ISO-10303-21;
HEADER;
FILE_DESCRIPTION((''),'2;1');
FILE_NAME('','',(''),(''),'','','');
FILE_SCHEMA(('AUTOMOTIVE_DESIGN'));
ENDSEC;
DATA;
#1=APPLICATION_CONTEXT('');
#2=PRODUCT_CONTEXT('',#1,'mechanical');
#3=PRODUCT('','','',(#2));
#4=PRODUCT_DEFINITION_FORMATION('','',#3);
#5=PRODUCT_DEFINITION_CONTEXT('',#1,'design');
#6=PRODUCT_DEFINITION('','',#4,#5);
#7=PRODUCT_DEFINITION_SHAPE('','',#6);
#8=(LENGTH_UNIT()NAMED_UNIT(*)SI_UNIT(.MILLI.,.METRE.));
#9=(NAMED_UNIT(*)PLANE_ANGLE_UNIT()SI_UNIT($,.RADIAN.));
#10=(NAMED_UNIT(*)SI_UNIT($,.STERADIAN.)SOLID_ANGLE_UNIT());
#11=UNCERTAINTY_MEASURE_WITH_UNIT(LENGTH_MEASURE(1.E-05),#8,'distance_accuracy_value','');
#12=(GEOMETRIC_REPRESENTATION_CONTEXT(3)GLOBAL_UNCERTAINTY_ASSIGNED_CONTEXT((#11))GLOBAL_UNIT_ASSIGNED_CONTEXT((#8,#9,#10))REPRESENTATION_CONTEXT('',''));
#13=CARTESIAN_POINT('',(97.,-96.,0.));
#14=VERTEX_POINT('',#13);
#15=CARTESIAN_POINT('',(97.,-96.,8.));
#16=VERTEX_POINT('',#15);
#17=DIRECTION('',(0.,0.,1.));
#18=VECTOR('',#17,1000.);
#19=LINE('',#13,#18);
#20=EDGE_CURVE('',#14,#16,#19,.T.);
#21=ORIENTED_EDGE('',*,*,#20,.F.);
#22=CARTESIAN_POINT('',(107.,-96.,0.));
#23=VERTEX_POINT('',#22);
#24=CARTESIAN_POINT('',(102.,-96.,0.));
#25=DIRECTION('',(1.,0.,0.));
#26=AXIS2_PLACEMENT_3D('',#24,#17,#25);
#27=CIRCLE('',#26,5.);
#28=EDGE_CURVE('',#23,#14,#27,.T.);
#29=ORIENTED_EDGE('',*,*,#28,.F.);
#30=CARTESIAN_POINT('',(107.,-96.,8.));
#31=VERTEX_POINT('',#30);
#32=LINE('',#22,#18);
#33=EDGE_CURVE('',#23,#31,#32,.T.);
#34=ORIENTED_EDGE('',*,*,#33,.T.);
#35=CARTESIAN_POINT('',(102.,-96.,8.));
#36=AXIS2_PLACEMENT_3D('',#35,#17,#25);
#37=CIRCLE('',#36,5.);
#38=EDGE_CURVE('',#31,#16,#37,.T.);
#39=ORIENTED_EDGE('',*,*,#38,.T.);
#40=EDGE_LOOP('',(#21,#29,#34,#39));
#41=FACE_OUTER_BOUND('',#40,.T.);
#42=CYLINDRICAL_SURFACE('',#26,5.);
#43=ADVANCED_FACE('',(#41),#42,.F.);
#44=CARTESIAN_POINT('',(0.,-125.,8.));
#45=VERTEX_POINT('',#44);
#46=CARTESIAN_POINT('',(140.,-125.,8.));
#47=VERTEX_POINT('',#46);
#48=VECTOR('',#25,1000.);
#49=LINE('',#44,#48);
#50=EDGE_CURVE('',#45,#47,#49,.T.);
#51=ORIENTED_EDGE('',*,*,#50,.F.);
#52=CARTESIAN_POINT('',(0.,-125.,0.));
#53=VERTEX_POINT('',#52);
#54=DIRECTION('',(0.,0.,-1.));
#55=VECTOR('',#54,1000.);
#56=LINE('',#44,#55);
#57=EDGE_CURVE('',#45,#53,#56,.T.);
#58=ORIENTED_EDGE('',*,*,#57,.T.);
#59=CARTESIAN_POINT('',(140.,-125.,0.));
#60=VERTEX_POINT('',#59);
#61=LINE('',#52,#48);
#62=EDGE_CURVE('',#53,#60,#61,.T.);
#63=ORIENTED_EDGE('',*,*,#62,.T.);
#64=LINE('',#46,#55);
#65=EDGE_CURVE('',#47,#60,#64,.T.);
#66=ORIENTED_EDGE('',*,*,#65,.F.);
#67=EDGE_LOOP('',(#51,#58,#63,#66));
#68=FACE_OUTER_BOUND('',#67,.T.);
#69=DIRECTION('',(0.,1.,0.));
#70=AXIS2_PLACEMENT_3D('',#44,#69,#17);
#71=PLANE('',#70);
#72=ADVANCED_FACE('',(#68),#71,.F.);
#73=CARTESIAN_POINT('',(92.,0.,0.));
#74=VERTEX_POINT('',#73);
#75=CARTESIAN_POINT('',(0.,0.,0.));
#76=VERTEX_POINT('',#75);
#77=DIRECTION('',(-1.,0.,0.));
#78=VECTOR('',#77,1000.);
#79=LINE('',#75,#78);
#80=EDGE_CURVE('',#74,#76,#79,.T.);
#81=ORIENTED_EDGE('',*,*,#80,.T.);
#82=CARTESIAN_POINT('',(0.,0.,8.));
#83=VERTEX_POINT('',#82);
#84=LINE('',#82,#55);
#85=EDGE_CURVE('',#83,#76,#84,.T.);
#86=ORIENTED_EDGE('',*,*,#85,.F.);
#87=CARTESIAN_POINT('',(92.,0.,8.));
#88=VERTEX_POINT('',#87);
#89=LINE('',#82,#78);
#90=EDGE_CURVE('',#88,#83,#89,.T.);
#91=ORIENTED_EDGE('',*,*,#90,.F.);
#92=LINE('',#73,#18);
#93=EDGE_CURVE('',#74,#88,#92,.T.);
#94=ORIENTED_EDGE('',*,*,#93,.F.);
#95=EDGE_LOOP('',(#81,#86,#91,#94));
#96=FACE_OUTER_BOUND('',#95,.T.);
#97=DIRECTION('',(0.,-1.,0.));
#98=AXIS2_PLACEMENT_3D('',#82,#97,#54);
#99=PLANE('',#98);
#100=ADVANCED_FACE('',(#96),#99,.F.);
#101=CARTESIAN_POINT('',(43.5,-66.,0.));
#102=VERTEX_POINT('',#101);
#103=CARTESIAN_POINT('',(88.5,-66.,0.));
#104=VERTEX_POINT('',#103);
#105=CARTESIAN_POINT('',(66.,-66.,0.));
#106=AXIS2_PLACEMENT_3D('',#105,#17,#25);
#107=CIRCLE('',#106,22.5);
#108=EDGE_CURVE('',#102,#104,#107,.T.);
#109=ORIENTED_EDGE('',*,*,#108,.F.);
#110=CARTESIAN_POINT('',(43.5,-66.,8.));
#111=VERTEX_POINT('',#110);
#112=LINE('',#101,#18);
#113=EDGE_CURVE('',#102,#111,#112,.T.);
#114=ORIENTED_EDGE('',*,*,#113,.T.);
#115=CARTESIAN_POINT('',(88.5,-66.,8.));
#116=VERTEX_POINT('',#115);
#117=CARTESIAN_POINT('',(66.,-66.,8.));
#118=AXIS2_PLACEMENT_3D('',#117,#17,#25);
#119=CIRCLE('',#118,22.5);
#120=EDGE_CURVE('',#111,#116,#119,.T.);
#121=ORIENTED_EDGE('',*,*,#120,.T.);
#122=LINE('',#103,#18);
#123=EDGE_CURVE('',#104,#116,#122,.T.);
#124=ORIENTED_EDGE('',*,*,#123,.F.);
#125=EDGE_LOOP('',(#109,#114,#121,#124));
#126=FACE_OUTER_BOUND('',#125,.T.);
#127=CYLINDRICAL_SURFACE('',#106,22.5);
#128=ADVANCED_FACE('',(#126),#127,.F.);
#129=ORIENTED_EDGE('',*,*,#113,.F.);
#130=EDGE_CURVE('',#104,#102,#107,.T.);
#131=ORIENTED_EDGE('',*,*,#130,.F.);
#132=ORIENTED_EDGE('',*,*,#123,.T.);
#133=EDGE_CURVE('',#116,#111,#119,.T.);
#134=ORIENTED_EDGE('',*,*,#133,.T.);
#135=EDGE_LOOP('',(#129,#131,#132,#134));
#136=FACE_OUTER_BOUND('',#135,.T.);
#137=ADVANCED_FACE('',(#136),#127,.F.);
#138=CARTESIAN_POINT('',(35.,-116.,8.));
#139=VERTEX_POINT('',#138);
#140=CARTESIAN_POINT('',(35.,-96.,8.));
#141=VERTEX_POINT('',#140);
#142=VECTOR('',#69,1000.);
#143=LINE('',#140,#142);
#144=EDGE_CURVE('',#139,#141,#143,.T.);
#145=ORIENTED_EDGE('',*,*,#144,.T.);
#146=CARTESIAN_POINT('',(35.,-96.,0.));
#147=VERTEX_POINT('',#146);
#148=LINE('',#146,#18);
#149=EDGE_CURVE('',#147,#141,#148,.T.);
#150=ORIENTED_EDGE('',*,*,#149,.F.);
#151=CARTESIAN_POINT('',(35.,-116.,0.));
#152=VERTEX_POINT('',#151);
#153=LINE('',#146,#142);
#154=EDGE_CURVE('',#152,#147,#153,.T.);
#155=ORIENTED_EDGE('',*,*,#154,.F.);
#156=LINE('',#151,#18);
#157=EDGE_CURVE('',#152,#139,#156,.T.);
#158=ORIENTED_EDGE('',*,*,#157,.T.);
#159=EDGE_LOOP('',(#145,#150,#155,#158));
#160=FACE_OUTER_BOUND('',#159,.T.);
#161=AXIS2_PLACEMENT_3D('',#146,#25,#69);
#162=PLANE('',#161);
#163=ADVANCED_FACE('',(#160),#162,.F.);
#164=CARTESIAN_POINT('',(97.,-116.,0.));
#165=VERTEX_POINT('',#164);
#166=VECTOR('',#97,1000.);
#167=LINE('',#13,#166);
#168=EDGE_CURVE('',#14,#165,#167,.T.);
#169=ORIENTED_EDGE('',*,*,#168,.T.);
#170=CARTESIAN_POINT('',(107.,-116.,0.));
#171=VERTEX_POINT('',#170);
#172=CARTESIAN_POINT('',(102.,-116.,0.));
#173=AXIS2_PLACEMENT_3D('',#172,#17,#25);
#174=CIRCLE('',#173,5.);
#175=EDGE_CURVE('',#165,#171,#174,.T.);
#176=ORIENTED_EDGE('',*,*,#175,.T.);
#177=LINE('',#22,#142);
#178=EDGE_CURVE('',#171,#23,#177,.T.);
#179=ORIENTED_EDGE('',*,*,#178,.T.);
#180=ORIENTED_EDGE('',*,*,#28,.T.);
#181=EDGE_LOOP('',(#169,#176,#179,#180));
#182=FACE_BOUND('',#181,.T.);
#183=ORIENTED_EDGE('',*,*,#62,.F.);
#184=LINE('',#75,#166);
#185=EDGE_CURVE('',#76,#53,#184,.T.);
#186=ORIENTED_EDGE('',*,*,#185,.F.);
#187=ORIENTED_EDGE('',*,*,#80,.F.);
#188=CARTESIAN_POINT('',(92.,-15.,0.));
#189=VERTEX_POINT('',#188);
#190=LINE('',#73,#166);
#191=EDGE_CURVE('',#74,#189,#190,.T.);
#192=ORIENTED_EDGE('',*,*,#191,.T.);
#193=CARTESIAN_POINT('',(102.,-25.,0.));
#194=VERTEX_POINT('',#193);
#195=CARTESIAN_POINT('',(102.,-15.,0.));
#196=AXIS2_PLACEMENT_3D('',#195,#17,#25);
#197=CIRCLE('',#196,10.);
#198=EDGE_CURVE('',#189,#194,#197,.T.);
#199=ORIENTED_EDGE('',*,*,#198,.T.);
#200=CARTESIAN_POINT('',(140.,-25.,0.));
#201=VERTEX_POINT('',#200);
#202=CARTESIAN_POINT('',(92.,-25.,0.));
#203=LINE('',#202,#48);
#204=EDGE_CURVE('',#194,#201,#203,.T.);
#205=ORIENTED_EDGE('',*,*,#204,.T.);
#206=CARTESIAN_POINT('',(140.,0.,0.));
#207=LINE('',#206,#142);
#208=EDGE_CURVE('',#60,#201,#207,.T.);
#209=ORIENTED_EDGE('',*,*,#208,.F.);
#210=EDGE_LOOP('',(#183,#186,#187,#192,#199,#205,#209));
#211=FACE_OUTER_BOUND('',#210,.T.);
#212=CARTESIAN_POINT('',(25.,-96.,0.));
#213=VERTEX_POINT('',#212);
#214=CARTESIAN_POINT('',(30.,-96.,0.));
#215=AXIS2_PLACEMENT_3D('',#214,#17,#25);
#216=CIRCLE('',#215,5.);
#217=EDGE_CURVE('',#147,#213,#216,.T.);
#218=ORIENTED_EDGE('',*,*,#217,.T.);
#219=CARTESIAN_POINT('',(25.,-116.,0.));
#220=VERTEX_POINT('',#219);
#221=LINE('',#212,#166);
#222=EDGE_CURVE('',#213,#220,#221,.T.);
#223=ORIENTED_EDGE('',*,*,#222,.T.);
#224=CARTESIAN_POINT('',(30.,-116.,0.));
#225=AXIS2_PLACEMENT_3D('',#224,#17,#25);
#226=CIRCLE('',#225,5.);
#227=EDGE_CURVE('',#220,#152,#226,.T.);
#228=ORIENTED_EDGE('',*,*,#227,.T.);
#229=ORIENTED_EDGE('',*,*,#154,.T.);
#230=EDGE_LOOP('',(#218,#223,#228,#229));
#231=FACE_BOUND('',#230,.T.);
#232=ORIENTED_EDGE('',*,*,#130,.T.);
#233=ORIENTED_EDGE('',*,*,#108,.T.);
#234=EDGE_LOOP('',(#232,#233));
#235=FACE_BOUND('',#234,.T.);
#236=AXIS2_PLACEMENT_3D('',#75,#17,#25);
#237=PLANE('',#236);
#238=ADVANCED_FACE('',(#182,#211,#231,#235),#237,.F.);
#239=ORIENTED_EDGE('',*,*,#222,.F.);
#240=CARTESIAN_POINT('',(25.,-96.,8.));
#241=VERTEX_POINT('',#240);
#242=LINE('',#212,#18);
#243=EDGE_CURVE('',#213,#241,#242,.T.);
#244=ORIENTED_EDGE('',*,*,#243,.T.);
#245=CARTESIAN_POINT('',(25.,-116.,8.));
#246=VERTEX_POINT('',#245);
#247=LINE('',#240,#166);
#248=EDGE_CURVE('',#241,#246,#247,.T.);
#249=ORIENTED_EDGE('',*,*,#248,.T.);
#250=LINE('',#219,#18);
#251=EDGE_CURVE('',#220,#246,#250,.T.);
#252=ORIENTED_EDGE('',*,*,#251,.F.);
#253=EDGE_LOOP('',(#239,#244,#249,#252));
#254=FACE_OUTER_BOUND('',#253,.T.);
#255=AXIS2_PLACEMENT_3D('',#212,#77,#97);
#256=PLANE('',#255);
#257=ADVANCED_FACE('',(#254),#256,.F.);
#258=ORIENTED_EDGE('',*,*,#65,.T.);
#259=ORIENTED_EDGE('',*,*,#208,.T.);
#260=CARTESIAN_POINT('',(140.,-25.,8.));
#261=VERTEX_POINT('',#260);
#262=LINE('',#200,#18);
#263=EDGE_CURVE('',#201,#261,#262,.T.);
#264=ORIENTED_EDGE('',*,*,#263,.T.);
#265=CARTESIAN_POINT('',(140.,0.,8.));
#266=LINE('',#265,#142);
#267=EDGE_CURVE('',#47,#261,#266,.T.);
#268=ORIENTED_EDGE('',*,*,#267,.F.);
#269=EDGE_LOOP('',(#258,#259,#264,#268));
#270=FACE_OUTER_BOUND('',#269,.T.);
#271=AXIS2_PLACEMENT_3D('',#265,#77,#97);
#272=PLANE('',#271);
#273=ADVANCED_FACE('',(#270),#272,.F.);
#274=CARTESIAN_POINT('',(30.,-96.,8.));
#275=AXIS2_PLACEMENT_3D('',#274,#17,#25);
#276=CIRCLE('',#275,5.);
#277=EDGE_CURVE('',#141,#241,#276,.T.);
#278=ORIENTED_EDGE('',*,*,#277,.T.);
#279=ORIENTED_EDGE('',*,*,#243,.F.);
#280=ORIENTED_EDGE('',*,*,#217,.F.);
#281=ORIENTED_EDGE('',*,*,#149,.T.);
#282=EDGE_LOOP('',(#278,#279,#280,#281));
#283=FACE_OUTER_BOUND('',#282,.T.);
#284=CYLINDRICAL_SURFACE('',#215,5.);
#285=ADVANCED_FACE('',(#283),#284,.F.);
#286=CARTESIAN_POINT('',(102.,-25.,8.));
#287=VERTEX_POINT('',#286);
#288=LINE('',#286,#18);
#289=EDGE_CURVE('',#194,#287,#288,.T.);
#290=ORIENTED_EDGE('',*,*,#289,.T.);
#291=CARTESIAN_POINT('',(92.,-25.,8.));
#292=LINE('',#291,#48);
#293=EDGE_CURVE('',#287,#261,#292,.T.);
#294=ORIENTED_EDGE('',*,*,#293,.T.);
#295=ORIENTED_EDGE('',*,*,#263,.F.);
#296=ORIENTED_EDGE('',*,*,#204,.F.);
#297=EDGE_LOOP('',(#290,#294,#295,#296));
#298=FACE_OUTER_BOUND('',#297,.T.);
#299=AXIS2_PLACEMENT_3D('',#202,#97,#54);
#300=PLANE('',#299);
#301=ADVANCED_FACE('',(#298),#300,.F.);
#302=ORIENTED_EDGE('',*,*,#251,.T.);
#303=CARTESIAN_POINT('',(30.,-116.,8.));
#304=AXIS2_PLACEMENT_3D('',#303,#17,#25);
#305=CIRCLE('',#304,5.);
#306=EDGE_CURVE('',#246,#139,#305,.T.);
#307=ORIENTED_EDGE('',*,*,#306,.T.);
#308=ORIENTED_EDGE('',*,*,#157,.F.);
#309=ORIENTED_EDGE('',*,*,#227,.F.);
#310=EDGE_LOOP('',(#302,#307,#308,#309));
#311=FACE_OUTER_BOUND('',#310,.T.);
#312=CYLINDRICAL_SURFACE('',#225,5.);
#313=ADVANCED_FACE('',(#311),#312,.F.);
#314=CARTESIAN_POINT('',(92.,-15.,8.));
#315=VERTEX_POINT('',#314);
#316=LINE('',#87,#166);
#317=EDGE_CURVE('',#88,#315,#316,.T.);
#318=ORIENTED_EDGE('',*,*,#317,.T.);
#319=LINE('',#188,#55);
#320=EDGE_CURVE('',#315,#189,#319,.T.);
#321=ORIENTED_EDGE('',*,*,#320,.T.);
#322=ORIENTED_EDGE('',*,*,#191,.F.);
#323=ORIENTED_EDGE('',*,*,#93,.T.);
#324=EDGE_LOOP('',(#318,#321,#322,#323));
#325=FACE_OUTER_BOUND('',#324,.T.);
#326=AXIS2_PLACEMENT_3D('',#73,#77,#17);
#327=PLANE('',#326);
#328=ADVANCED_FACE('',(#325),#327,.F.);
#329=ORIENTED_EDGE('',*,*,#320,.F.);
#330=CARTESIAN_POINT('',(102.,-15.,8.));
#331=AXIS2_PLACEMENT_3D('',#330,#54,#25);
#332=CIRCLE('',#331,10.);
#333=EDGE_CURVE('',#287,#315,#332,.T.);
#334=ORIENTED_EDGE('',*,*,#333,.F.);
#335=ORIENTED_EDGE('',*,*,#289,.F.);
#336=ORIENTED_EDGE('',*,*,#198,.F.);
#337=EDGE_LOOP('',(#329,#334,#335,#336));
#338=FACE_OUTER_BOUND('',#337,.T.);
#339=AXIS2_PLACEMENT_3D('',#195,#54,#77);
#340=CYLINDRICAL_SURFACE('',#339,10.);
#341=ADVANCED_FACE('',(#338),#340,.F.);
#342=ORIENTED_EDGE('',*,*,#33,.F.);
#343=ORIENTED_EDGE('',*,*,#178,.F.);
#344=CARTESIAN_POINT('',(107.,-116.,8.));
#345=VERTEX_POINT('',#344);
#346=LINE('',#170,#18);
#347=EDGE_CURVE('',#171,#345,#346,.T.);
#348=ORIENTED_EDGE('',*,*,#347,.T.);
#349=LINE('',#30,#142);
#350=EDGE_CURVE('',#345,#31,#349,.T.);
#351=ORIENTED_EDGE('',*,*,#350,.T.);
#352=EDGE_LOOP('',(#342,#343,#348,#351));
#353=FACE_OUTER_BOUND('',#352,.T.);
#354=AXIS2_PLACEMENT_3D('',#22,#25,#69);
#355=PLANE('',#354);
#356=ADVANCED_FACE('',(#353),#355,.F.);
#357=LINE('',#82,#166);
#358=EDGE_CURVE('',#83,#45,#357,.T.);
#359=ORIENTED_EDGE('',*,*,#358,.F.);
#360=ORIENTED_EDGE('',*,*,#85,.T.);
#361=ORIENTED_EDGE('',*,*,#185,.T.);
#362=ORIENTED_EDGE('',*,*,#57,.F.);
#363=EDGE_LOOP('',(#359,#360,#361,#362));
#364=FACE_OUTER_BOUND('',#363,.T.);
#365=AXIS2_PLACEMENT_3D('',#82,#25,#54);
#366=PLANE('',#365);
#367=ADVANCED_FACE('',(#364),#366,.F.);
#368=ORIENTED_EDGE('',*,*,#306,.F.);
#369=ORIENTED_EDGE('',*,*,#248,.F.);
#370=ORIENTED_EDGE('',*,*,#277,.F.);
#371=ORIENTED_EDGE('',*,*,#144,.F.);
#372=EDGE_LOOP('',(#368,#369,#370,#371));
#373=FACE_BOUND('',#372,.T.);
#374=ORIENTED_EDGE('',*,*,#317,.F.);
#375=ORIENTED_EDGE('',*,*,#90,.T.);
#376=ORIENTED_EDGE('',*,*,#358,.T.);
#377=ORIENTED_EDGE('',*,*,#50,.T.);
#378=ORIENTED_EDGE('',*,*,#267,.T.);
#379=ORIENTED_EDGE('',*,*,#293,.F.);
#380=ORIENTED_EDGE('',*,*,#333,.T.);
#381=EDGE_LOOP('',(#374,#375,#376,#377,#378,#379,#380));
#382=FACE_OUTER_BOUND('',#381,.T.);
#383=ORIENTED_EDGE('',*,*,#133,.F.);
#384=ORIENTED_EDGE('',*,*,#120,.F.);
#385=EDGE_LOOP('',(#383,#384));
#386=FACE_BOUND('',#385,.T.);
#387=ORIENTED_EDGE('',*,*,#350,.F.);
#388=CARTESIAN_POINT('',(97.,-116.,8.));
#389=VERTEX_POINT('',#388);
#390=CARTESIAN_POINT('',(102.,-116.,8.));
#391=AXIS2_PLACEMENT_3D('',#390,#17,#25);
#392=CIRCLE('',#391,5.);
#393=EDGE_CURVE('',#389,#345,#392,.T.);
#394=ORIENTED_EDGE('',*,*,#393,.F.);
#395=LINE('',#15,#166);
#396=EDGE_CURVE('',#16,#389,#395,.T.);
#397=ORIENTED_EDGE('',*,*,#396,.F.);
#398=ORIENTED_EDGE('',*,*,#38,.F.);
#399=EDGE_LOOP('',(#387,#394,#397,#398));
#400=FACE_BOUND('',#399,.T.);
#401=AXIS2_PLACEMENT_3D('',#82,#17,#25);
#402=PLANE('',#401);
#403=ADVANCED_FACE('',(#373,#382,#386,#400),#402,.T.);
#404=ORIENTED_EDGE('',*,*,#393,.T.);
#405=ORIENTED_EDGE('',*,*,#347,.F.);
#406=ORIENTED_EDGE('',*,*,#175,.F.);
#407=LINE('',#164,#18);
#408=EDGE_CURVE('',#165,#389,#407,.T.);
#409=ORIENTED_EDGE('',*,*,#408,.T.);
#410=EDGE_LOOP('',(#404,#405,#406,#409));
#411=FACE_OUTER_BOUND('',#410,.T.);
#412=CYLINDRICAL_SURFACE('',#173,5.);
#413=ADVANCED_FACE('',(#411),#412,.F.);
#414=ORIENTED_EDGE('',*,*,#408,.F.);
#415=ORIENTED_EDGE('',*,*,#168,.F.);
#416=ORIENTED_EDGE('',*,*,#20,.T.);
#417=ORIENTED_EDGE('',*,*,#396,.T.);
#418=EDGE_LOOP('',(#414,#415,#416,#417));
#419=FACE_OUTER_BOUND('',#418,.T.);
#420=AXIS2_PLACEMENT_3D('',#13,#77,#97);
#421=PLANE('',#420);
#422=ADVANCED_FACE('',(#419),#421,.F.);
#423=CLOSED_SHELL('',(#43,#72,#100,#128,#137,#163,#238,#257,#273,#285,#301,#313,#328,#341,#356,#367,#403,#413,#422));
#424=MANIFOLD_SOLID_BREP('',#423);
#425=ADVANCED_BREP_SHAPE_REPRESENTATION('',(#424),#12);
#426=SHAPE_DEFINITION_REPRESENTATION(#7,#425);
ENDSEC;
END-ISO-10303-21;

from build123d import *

# Parameters (mm, degrees)
SKETCH1_W           = 140
SKETCH1_H           = 125
BOSS_EXTRUDE1_DEPTH = 8
SKETCH2_R           = 22.5
CUT_EXTRUDE1_DEPTH  = 8
CUT_EXTRUDE2_DEPTH  = 8
LPATTERN1_COUNT     = 2
LPATTERN1_PITCH     = 72
SKETCH4_W           = 48
SKETCH4_H           = 25
CUT_EXTRUDE3_DEPTH  = 8
FILLET1_R           = 10


with BuildPart() as part:
    # Sketch1 → Boss-Extrude1 (new body)
    with BuildSketch(Plane.XY):
        with Locations((70, -62.5)):
            Rectangle(SKETCH1_W, SKETCH1_H)
    extrude(amount=BOSS_EXTRUDE1_DEPTH)

    # Sketch2 → Cut-Extrude1 (cut)
    with BuildSketch(Plane.XY.offset(8)):
        with Locations((66, -66)):
            Circle(SKETCH2_R)
    extrude(amount=-CUT_EXTRUDE1_DEPTH, mode=Mode.SUBTRACT)

    # Sketch3 → Cut-Extrude2 (cut)
    with BuildSketch(Plane.XY.offset(8)):
        with BuildLine():
            Line((35, -96), (35, -116))
            ThreePointArc((35, -116), (30, -121), (25, -116))
            Line((25, -116), (25, -96))
            ThreePointArc((25, -96), (30, -91), (35, -96))
        make_face()
    cut_extrude2 = extrude(amount=-CUT_EXTRUDE2_DEPTH, mode=Mode.SUBTRACT)

    # LPattern1: Cut-Extrude2 ×2
    with Locations(*[(i * LPATTERN1_PITCH, 0, 0) for i in range(1, LPATTERN1_COUNT)]):
        add(cut_extrude2, mode=Mode.SUBTRACT)

    # Sketch4 → Cut-Extrude3 (cut)
    with BuildSketch(Plane.XY.offset(8)):
        with Locations((116, -12.5)):
            Rectangle(SKETCH4_W, SKETCH4_H)
    extrude(amount=-CUT_EXTRUDE3_DEPTH, mode=Mode.SUBTRACT)

    # Fillet1
    fillet1_edges = [part.edges().sort_by_distance(p)[0] for p in [
        (92, -25, 4),
    ]]
    fillet(fillet1_edges, radius=FILLET1_R)


solid = part.part
